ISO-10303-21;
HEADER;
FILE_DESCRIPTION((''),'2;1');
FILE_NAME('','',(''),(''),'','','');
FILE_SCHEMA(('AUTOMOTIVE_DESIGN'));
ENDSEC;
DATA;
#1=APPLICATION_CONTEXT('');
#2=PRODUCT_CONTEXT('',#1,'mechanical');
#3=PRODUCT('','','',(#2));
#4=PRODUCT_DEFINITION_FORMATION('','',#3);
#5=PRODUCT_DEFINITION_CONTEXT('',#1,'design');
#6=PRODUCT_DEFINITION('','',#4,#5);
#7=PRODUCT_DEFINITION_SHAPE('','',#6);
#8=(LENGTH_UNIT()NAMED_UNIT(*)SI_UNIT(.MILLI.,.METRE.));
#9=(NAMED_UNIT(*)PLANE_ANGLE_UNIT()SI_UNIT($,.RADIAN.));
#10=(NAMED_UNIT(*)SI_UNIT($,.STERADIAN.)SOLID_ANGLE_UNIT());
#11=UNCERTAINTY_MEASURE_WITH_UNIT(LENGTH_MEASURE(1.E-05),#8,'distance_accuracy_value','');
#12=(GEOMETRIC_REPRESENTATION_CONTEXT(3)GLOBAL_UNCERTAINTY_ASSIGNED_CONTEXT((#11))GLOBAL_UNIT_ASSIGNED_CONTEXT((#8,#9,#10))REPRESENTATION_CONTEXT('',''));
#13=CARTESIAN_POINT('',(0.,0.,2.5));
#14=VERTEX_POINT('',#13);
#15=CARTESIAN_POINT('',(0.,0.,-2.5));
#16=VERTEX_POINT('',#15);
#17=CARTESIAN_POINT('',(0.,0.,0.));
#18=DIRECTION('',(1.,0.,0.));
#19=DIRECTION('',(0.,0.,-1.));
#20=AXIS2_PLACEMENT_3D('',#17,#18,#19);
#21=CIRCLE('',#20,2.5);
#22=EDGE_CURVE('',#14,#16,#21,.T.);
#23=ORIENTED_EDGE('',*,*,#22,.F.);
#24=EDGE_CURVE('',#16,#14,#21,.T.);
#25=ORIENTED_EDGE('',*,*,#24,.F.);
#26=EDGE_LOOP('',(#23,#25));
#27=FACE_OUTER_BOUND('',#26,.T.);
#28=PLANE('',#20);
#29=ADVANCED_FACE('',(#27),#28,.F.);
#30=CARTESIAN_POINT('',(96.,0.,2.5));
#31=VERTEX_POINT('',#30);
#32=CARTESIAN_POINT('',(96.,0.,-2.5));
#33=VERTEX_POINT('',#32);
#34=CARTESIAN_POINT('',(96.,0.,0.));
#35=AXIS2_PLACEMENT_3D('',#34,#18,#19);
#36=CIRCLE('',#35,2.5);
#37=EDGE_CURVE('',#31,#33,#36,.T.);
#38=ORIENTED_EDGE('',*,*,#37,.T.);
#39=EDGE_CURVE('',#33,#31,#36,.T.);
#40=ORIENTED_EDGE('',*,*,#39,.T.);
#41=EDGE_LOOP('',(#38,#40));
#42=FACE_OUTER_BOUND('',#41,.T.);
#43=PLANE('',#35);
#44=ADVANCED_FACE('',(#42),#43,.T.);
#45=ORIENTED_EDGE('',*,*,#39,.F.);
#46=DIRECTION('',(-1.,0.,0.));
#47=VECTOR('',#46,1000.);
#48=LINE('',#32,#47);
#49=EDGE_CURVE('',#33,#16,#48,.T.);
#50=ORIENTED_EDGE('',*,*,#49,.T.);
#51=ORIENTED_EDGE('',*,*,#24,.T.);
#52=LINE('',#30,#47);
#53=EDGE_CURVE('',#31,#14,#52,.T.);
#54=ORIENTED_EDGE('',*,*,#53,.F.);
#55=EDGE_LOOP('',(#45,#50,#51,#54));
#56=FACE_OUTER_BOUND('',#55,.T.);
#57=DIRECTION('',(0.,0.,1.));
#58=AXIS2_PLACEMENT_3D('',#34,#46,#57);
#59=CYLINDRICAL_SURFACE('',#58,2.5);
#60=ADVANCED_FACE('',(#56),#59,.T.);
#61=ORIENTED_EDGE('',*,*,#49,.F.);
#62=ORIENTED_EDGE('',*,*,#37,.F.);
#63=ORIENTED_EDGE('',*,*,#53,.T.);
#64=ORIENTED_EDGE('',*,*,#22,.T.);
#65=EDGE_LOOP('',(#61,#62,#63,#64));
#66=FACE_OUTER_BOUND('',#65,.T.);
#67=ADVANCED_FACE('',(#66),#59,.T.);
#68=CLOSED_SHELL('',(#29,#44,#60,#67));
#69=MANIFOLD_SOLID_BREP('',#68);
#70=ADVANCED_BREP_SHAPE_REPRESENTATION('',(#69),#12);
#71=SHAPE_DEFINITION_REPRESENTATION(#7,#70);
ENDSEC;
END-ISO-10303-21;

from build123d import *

# Parameters (mm, degrees)
ROD_PROFILE_5_R = 2.5
ROD_5X96_DEPTH  = 96


with BuildPart() as part:
    # Rod Profile Ø5 → Rod Ø5x96 (new body)
    with BuildSketch(Plane(origin=(0, 0, 0), x_dir=(0, 0, -1), z_dir=(1, 0, 0))):
        Circle(ROD_PROFILE_5_R)
    extrude(amount=ROD_5X96_DEPTH)


solid = part.part
